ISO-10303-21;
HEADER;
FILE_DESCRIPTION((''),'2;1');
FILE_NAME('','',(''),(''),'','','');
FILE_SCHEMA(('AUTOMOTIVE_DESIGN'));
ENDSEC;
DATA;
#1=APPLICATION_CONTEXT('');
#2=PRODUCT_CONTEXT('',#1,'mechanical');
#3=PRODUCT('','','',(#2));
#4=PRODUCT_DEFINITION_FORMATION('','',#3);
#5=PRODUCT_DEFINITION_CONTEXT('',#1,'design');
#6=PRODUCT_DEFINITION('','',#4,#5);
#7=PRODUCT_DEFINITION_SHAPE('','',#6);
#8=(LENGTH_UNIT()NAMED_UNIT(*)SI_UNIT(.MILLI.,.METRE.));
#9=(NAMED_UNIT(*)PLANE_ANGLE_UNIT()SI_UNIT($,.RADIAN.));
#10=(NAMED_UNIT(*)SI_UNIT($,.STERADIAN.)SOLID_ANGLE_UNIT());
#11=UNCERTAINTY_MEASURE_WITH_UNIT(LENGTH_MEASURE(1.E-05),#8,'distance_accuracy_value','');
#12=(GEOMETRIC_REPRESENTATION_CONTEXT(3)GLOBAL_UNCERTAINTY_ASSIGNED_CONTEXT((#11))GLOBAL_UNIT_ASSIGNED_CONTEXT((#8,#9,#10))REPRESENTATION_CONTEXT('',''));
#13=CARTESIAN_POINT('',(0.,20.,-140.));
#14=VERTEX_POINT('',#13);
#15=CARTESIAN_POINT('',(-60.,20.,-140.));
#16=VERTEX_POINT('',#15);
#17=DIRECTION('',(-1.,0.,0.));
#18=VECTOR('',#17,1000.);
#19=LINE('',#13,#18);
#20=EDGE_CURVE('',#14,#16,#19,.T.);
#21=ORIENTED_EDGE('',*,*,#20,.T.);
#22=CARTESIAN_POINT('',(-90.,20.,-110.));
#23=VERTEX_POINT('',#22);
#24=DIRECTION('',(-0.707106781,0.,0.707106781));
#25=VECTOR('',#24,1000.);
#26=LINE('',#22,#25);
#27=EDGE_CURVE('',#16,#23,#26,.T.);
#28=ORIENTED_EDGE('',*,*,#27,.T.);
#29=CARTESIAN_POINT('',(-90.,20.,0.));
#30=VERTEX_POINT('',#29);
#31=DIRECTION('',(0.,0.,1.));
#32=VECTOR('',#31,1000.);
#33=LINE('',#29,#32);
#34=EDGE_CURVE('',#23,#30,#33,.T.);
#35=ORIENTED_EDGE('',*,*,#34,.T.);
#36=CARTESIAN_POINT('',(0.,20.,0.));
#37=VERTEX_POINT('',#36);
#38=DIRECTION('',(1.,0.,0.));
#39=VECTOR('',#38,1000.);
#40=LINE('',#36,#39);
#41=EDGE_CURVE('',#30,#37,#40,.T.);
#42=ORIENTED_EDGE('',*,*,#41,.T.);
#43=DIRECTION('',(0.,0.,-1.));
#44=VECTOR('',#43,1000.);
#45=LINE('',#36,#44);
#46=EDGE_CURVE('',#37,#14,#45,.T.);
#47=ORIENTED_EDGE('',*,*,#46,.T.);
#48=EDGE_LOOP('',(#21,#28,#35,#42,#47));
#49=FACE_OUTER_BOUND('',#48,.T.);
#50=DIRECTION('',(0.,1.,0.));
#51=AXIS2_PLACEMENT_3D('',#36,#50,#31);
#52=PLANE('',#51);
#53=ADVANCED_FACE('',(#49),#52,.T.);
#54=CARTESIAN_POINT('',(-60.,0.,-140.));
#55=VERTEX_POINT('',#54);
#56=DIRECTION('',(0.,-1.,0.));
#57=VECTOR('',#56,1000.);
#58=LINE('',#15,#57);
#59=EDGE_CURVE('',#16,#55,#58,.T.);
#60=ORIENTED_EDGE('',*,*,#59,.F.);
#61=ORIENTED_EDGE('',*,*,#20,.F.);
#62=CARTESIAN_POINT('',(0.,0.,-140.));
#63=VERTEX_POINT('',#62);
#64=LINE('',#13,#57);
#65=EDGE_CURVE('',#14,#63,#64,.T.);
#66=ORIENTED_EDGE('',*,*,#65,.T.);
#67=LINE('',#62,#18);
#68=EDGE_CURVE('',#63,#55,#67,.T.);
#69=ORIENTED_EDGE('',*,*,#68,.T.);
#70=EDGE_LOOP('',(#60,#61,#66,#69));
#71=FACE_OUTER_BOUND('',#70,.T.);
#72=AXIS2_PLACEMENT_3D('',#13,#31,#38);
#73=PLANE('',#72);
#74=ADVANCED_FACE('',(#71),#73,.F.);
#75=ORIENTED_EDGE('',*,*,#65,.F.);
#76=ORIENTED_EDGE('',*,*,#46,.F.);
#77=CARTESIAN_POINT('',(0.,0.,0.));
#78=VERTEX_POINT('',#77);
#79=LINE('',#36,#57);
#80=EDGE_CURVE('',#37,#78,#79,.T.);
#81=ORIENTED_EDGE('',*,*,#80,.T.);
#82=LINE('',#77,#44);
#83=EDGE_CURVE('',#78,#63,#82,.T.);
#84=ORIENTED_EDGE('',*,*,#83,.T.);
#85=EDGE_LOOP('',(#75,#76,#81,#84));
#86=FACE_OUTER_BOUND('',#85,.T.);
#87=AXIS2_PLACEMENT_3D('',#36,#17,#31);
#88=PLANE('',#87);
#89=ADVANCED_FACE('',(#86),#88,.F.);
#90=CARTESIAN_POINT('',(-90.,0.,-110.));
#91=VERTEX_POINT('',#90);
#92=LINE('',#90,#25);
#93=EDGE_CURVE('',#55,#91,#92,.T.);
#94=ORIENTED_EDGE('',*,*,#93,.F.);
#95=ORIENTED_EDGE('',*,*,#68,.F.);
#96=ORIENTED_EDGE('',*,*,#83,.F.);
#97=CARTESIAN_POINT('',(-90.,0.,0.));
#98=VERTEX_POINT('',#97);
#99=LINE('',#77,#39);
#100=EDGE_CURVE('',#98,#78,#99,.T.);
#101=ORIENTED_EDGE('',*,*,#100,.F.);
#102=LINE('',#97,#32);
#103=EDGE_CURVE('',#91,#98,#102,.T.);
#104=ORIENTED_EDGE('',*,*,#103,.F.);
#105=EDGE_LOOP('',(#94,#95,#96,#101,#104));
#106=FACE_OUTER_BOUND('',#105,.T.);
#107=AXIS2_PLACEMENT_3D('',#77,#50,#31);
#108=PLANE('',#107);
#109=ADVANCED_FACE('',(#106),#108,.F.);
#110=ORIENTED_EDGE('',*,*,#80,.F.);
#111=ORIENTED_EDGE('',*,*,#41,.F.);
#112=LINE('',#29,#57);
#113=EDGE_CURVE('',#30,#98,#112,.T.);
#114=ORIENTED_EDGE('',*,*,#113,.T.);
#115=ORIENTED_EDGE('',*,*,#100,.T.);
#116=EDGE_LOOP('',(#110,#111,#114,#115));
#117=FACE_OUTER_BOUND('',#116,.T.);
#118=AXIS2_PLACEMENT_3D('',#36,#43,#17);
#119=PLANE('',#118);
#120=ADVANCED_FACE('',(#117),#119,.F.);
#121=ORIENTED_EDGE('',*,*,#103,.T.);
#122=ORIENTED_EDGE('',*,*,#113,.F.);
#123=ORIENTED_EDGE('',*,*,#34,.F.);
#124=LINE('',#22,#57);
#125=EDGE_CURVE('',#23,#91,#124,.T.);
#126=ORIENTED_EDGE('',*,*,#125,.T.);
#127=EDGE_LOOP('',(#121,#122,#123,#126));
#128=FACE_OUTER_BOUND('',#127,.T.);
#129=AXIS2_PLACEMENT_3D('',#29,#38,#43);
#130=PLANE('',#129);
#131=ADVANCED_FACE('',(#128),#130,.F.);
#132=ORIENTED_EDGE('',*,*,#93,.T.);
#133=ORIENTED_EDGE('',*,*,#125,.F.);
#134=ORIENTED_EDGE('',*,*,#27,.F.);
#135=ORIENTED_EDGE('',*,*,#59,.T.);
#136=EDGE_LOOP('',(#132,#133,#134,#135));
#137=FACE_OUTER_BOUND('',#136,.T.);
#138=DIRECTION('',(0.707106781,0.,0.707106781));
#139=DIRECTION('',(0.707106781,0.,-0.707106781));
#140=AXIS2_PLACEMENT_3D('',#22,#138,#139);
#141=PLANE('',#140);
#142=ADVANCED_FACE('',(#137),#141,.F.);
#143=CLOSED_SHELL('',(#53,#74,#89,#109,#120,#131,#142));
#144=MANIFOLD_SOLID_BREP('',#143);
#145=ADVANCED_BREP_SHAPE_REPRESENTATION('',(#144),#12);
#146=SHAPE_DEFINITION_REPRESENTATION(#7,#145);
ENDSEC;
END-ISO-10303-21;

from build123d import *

# Parameters (mm, degrees)
BOSS_EXTRUDE1_DEPTH = 20


with BuildPart() as part:
    # Sketch1 → Boss-Extrude1 (new body)
    with BuildSketch(Plane(origin=(0, 0, 0), x_dir=(1, 0, 0), z_dir=(0, 1, 0))):
        Polygon((-90, 110), (-60, 140), (0, 140), (0, 0), (-90, 0), align=None)
    extrude(amount=BOSS_EXTRUDE1_DEPTH)


solid = part.part
